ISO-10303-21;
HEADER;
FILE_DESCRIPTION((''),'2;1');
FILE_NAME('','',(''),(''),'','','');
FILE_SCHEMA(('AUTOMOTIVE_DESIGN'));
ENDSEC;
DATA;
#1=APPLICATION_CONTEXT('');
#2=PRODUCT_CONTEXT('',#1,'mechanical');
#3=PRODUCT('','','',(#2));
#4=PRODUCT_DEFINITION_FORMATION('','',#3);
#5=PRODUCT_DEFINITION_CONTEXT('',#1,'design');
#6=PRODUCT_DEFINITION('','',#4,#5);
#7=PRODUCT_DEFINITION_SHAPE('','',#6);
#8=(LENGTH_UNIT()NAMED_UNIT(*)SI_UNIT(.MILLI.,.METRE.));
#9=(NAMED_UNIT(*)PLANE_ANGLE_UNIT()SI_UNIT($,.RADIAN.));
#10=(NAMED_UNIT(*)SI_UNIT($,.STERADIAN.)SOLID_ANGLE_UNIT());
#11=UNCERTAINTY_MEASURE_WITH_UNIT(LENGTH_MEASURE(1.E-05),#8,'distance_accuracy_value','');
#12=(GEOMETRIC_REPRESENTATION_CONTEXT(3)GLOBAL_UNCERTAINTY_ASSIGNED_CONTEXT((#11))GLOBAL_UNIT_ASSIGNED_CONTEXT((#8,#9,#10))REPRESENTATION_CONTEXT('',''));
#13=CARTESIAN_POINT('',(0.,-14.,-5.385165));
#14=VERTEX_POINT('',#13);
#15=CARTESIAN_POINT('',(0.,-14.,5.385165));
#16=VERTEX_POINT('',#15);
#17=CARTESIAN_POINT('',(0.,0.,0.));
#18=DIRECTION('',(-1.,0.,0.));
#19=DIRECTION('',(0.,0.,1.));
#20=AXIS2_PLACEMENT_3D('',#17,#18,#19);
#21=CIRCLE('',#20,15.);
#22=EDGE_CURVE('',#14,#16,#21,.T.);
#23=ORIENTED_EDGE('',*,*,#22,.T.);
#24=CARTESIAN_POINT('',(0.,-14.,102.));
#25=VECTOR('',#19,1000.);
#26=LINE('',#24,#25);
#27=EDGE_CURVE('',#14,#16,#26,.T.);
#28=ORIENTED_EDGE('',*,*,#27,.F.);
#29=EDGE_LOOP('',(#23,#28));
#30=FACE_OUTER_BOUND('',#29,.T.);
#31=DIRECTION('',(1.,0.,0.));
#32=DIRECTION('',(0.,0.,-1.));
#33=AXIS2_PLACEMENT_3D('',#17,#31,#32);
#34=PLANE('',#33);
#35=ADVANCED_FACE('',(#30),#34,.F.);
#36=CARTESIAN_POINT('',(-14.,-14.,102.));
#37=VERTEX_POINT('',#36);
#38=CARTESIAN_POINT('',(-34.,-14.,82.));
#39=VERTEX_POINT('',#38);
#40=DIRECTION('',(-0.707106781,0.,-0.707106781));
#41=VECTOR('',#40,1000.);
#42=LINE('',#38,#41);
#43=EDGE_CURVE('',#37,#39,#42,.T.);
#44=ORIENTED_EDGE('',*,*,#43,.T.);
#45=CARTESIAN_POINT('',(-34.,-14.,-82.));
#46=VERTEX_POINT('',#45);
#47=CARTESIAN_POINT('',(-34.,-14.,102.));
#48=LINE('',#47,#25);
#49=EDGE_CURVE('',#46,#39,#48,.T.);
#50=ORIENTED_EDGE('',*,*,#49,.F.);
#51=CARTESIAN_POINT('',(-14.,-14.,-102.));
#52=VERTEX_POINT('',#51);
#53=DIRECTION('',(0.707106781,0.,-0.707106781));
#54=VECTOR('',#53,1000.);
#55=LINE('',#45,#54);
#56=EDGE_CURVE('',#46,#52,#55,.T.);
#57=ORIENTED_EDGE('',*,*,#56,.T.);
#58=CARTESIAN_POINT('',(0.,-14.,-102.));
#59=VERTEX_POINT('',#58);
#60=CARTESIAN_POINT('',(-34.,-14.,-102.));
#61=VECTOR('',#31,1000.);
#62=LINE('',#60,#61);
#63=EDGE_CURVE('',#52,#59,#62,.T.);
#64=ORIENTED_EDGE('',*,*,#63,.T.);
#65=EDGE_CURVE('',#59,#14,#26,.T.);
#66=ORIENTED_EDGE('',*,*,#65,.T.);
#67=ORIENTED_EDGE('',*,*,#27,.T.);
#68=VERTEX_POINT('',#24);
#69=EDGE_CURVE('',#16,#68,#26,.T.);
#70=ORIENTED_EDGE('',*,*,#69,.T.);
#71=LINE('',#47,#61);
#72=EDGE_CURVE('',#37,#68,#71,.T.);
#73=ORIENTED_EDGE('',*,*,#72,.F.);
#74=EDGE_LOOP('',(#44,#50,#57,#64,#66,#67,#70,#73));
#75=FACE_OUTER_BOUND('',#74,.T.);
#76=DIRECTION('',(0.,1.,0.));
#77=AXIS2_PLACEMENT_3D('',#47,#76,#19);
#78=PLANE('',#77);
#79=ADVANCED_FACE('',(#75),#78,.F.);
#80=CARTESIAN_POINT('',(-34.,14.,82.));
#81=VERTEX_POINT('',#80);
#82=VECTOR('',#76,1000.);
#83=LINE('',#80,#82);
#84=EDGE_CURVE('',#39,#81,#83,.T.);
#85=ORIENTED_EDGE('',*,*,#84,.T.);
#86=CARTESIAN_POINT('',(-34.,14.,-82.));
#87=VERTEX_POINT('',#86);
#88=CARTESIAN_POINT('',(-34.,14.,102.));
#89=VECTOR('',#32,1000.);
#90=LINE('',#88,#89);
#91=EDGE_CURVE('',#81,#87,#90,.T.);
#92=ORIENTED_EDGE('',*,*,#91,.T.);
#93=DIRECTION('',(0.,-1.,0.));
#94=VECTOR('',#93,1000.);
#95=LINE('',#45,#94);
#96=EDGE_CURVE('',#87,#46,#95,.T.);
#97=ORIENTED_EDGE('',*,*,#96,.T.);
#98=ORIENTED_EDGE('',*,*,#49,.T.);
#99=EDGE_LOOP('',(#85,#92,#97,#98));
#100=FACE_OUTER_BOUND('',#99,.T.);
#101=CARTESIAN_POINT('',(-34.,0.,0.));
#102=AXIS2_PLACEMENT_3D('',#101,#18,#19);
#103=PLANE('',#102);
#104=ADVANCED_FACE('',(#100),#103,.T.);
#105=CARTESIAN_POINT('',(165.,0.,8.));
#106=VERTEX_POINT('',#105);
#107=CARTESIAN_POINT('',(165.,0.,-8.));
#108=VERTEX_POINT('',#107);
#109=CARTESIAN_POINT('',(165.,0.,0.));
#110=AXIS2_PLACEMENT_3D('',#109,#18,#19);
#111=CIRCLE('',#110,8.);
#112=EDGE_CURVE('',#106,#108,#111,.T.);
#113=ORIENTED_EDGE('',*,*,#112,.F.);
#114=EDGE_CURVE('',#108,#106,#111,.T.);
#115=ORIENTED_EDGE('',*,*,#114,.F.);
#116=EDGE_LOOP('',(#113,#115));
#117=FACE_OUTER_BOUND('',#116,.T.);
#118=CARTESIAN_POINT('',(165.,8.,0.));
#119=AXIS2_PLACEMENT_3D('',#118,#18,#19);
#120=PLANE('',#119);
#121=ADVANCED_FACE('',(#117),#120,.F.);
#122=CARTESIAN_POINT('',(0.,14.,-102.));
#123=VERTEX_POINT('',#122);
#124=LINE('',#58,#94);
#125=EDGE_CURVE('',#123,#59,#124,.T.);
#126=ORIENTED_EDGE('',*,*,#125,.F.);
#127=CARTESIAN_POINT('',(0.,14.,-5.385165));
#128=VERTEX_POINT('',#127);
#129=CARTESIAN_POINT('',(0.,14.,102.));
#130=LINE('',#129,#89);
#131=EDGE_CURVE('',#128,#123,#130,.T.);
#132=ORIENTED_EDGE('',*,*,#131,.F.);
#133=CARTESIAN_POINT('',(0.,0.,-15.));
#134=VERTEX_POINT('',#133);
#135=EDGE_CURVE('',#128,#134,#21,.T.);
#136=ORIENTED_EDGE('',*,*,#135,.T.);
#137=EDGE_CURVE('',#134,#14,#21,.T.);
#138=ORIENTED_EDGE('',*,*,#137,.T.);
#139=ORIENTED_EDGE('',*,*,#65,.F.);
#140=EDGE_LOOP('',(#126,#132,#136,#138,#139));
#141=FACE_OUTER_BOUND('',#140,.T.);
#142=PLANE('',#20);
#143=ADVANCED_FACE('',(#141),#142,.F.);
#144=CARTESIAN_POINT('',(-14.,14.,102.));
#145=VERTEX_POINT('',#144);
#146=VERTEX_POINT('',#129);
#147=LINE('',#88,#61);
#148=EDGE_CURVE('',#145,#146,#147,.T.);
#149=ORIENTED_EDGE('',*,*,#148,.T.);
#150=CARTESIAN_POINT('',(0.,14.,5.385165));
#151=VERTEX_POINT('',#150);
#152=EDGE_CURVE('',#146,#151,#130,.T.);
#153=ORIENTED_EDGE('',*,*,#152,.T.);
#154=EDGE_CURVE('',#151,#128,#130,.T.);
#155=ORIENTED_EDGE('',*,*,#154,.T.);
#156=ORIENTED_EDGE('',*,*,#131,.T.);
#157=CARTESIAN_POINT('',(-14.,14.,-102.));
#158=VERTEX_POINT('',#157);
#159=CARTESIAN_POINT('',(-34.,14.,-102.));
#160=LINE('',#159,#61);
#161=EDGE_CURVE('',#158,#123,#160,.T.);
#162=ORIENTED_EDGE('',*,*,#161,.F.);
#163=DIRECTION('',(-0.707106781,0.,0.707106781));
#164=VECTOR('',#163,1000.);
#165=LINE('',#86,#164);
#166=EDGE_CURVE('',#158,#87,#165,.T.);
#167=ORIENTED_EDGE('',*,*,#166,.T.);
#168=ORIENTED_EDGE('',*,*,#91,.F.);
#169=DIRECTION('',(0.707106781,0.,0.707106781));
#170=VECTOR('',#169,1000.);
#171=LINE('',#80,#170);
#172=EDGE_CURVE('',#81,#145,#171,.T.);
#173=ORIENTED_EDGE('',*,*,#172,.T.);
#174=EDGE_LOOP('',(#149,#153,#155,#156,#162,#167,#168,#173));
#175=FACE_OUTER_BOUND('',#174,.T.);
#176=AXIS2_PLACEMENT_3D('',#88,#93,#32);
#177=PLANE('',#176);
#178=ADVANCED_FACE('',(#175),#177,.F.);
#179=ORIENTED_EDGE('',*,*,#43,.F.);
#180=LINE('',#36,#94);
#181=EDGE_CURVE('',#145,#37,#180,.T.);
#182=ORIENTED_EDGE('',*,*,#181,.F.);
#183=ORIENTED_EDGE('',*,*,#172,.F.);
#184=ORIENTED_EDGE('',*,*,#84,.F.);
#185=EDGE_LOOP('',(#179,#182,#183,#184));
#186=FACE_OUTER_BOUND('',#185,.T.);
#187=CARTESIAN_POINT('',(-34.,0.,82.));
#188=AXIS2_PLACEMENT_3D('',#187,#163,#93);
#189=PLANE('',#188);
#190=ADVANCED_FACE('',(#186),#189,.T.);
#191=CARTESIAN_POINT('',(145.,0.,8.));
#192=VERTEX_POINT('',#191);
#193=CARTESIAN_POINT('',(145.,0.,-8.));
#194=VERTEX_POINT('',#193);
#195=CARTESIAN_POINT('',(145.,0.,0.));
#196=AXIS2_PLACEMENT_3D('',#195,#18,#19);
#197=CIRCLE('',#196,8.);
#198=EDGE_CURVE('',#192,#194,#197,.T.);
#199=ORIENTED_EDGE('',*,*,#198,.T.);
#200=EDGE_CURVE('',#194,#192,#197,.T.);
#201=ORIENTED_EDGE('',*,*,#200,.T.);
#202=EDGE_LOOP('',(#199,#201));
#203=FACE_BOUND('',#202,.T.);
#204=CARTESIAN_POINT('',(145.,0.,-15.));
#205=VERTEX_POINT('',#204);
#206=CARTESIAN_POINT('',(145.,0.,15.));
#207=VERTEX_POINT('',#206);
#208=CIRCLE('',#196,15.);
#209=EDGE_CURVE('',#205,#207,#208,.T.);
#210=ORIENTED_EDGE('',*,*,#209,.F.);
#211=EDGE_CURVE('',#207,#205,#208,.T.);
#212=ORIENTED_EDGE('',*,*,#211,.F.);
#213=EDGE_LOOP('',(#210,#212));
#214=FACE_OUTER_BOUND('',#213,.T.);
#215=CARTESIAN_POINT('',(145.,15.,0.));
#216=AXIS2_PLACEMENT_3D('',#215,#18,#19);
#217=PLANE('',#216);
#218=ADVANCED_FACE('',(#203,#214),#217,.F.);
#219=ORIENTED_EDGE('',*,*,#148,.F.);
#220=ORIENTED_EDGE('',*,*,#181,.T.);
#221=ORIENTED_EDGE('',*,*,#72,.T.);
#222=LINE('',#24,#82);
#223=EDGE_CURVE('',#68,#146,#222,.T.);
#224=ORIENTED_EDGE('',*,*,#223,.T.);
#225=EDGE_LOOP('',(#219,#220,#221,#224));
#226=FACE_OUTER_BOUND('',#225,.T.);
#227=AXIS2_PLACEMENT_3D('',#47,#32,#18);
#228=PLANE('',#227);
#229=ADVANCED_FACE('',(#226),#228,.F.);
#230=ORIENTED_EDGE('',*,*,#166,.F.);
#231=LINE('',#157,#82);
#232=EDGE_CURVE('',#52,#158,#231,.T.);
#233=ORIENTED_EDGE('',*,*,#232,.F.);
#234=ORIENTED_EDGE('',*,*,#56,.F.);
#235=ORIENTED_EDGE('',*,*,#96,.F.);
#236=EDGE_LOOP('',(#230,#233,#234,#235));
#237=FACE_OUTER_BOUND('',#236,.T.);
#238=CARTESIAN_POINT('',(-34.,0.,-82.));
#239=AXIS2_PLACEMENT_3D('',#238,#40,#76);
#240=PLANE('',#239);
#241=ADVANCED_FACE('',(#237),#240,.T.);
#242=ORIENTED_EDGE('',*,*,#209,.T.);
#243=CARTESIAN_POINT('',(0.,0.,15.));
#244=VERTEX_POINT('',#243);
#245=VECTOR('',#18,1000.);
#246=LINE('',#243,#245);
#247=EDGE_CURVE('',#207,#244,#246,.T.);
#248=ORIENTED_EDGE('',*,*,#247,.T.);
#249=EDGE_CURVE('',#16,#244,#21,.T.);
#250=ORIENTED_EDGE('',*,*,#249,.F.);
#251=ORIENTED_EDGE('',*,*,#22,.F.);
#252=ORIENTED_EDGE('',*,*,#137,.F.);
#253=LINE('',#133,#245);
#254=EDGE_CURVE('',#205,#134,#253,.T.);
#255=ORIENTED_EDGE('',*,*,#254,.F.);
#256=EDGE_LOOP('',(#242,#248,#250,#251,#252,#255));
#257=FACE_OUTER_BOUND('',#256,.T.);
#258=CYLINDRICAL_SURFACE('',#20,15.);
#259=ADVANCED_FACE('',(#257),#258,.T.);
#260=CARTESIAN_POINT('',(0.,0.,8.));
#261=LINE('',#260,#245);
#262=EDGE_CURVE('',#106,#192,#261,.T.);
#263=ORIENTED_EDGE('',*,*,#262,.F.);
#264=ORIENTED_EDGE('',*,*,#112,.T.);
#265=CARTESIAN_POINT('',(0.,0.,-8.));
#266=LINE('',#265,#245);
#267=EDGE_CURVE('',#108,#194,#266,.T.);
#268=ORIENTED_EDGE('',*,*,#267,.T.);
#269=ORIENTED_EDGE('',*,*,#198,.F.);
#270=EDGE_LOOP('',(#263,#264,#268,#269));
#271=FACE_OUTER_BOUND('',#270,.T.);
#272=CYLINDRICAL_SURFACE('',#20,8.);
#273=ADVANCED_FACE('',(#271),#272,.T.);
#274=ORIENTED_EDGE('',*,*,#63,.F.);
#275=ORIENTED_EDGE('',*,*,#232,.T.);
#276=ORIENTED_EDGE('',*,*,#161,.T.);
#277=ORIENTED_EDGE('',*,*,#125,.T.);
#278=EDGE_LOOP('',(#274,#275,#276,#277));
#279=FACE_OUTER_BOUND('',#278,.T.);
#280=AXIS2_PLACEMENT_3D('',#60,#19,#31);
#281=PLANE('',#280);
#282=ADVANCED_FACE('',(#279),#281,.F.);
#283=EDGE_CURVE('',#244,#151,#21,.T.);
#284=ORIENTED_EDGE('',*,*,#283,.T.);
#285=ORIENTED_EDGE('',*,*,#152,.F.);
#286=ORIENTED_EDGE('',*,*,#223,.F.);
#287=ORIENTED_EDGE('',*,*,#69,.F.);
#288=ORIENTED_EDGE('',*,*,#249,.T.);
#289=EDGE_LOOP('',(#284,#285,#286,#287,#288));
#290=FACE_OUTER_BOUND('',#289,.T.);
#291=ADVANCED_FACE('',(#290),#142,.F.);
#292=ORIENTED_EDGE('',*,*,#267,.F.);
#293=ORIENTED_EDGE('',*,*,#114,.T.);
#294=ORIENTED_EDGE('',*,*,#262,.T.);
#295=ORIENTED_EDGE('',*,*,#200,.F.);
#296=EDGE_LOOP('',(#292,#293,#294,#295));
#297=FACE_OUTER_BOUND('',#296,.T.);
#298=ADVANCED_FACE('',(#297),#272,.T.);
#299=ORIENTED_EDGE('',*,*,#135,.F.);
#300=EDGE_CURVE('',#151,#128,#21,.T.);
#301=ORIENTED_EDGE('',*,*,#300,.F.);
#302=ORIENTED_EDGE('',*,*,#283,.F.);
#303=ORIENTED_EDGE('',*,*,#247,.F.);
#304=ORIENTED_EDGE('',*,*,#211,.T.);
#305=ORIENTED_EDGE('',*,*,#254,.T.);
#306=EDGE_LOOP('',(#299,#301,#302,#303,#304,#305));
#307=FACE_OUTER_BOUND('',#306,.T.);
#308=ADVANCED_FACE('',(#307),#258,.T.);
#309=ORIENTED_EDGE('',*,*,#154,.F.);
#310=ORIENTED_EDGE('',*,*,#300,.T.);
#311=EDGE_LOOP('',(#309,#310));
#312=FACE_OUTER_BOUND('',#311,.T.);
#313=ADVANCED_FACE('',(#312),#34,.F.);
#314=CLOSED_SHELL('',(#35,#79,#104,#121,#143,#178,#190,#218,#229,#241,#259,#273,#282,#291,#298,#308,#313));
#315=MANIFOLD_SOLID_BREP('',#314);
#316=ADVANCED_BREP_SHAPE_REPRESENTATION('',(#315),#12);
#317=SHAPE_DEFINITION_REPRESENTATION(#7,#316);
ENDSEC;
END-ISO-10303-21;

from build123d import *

# Parameters (mm, degrees)
SKETCH2_W           = 204
SKETCH2_H           = 28
BOSS_EXTRUDE1_DEPTH = 34
CHAMFER1_SIZE       = 20


with BuildPart() as part:
    # Sketch1 → Revolve1 (revolve)
    with BuildSketch(Plane.XY, mode=Mode.PRIVATE) as revolve1_sk:
        Polygon((0, 0), (0, 15), (145, 15), (145, 8), (165, 8), (165, 0), align=None)
    revolve(revolve1_sk.sketch.rotate(Axis((0, 0, 0), (1, 0, 0)), 90), axis=Axis((0, 0, 0), (1, 0, 0)))

    # Sketch2 → Boss-Extrude1 (add)
    with BuildSketch(Plane.ZY):
        Rectangle(SKETCH2_W, SKETCH2_H)
    extrude(amount=BOSS_EXTRUDE1_DEPTH)

    # Chamfer1
    chamfer1_edges = [part.edges().sort_by_distance(p)[0] for p in [
        (-34, 0, -102),
        (-34, 0, 102),
    ]]
    chamfer(chamfer1_edges, length=CHAMFER1_SIZE)


solid = part.part
